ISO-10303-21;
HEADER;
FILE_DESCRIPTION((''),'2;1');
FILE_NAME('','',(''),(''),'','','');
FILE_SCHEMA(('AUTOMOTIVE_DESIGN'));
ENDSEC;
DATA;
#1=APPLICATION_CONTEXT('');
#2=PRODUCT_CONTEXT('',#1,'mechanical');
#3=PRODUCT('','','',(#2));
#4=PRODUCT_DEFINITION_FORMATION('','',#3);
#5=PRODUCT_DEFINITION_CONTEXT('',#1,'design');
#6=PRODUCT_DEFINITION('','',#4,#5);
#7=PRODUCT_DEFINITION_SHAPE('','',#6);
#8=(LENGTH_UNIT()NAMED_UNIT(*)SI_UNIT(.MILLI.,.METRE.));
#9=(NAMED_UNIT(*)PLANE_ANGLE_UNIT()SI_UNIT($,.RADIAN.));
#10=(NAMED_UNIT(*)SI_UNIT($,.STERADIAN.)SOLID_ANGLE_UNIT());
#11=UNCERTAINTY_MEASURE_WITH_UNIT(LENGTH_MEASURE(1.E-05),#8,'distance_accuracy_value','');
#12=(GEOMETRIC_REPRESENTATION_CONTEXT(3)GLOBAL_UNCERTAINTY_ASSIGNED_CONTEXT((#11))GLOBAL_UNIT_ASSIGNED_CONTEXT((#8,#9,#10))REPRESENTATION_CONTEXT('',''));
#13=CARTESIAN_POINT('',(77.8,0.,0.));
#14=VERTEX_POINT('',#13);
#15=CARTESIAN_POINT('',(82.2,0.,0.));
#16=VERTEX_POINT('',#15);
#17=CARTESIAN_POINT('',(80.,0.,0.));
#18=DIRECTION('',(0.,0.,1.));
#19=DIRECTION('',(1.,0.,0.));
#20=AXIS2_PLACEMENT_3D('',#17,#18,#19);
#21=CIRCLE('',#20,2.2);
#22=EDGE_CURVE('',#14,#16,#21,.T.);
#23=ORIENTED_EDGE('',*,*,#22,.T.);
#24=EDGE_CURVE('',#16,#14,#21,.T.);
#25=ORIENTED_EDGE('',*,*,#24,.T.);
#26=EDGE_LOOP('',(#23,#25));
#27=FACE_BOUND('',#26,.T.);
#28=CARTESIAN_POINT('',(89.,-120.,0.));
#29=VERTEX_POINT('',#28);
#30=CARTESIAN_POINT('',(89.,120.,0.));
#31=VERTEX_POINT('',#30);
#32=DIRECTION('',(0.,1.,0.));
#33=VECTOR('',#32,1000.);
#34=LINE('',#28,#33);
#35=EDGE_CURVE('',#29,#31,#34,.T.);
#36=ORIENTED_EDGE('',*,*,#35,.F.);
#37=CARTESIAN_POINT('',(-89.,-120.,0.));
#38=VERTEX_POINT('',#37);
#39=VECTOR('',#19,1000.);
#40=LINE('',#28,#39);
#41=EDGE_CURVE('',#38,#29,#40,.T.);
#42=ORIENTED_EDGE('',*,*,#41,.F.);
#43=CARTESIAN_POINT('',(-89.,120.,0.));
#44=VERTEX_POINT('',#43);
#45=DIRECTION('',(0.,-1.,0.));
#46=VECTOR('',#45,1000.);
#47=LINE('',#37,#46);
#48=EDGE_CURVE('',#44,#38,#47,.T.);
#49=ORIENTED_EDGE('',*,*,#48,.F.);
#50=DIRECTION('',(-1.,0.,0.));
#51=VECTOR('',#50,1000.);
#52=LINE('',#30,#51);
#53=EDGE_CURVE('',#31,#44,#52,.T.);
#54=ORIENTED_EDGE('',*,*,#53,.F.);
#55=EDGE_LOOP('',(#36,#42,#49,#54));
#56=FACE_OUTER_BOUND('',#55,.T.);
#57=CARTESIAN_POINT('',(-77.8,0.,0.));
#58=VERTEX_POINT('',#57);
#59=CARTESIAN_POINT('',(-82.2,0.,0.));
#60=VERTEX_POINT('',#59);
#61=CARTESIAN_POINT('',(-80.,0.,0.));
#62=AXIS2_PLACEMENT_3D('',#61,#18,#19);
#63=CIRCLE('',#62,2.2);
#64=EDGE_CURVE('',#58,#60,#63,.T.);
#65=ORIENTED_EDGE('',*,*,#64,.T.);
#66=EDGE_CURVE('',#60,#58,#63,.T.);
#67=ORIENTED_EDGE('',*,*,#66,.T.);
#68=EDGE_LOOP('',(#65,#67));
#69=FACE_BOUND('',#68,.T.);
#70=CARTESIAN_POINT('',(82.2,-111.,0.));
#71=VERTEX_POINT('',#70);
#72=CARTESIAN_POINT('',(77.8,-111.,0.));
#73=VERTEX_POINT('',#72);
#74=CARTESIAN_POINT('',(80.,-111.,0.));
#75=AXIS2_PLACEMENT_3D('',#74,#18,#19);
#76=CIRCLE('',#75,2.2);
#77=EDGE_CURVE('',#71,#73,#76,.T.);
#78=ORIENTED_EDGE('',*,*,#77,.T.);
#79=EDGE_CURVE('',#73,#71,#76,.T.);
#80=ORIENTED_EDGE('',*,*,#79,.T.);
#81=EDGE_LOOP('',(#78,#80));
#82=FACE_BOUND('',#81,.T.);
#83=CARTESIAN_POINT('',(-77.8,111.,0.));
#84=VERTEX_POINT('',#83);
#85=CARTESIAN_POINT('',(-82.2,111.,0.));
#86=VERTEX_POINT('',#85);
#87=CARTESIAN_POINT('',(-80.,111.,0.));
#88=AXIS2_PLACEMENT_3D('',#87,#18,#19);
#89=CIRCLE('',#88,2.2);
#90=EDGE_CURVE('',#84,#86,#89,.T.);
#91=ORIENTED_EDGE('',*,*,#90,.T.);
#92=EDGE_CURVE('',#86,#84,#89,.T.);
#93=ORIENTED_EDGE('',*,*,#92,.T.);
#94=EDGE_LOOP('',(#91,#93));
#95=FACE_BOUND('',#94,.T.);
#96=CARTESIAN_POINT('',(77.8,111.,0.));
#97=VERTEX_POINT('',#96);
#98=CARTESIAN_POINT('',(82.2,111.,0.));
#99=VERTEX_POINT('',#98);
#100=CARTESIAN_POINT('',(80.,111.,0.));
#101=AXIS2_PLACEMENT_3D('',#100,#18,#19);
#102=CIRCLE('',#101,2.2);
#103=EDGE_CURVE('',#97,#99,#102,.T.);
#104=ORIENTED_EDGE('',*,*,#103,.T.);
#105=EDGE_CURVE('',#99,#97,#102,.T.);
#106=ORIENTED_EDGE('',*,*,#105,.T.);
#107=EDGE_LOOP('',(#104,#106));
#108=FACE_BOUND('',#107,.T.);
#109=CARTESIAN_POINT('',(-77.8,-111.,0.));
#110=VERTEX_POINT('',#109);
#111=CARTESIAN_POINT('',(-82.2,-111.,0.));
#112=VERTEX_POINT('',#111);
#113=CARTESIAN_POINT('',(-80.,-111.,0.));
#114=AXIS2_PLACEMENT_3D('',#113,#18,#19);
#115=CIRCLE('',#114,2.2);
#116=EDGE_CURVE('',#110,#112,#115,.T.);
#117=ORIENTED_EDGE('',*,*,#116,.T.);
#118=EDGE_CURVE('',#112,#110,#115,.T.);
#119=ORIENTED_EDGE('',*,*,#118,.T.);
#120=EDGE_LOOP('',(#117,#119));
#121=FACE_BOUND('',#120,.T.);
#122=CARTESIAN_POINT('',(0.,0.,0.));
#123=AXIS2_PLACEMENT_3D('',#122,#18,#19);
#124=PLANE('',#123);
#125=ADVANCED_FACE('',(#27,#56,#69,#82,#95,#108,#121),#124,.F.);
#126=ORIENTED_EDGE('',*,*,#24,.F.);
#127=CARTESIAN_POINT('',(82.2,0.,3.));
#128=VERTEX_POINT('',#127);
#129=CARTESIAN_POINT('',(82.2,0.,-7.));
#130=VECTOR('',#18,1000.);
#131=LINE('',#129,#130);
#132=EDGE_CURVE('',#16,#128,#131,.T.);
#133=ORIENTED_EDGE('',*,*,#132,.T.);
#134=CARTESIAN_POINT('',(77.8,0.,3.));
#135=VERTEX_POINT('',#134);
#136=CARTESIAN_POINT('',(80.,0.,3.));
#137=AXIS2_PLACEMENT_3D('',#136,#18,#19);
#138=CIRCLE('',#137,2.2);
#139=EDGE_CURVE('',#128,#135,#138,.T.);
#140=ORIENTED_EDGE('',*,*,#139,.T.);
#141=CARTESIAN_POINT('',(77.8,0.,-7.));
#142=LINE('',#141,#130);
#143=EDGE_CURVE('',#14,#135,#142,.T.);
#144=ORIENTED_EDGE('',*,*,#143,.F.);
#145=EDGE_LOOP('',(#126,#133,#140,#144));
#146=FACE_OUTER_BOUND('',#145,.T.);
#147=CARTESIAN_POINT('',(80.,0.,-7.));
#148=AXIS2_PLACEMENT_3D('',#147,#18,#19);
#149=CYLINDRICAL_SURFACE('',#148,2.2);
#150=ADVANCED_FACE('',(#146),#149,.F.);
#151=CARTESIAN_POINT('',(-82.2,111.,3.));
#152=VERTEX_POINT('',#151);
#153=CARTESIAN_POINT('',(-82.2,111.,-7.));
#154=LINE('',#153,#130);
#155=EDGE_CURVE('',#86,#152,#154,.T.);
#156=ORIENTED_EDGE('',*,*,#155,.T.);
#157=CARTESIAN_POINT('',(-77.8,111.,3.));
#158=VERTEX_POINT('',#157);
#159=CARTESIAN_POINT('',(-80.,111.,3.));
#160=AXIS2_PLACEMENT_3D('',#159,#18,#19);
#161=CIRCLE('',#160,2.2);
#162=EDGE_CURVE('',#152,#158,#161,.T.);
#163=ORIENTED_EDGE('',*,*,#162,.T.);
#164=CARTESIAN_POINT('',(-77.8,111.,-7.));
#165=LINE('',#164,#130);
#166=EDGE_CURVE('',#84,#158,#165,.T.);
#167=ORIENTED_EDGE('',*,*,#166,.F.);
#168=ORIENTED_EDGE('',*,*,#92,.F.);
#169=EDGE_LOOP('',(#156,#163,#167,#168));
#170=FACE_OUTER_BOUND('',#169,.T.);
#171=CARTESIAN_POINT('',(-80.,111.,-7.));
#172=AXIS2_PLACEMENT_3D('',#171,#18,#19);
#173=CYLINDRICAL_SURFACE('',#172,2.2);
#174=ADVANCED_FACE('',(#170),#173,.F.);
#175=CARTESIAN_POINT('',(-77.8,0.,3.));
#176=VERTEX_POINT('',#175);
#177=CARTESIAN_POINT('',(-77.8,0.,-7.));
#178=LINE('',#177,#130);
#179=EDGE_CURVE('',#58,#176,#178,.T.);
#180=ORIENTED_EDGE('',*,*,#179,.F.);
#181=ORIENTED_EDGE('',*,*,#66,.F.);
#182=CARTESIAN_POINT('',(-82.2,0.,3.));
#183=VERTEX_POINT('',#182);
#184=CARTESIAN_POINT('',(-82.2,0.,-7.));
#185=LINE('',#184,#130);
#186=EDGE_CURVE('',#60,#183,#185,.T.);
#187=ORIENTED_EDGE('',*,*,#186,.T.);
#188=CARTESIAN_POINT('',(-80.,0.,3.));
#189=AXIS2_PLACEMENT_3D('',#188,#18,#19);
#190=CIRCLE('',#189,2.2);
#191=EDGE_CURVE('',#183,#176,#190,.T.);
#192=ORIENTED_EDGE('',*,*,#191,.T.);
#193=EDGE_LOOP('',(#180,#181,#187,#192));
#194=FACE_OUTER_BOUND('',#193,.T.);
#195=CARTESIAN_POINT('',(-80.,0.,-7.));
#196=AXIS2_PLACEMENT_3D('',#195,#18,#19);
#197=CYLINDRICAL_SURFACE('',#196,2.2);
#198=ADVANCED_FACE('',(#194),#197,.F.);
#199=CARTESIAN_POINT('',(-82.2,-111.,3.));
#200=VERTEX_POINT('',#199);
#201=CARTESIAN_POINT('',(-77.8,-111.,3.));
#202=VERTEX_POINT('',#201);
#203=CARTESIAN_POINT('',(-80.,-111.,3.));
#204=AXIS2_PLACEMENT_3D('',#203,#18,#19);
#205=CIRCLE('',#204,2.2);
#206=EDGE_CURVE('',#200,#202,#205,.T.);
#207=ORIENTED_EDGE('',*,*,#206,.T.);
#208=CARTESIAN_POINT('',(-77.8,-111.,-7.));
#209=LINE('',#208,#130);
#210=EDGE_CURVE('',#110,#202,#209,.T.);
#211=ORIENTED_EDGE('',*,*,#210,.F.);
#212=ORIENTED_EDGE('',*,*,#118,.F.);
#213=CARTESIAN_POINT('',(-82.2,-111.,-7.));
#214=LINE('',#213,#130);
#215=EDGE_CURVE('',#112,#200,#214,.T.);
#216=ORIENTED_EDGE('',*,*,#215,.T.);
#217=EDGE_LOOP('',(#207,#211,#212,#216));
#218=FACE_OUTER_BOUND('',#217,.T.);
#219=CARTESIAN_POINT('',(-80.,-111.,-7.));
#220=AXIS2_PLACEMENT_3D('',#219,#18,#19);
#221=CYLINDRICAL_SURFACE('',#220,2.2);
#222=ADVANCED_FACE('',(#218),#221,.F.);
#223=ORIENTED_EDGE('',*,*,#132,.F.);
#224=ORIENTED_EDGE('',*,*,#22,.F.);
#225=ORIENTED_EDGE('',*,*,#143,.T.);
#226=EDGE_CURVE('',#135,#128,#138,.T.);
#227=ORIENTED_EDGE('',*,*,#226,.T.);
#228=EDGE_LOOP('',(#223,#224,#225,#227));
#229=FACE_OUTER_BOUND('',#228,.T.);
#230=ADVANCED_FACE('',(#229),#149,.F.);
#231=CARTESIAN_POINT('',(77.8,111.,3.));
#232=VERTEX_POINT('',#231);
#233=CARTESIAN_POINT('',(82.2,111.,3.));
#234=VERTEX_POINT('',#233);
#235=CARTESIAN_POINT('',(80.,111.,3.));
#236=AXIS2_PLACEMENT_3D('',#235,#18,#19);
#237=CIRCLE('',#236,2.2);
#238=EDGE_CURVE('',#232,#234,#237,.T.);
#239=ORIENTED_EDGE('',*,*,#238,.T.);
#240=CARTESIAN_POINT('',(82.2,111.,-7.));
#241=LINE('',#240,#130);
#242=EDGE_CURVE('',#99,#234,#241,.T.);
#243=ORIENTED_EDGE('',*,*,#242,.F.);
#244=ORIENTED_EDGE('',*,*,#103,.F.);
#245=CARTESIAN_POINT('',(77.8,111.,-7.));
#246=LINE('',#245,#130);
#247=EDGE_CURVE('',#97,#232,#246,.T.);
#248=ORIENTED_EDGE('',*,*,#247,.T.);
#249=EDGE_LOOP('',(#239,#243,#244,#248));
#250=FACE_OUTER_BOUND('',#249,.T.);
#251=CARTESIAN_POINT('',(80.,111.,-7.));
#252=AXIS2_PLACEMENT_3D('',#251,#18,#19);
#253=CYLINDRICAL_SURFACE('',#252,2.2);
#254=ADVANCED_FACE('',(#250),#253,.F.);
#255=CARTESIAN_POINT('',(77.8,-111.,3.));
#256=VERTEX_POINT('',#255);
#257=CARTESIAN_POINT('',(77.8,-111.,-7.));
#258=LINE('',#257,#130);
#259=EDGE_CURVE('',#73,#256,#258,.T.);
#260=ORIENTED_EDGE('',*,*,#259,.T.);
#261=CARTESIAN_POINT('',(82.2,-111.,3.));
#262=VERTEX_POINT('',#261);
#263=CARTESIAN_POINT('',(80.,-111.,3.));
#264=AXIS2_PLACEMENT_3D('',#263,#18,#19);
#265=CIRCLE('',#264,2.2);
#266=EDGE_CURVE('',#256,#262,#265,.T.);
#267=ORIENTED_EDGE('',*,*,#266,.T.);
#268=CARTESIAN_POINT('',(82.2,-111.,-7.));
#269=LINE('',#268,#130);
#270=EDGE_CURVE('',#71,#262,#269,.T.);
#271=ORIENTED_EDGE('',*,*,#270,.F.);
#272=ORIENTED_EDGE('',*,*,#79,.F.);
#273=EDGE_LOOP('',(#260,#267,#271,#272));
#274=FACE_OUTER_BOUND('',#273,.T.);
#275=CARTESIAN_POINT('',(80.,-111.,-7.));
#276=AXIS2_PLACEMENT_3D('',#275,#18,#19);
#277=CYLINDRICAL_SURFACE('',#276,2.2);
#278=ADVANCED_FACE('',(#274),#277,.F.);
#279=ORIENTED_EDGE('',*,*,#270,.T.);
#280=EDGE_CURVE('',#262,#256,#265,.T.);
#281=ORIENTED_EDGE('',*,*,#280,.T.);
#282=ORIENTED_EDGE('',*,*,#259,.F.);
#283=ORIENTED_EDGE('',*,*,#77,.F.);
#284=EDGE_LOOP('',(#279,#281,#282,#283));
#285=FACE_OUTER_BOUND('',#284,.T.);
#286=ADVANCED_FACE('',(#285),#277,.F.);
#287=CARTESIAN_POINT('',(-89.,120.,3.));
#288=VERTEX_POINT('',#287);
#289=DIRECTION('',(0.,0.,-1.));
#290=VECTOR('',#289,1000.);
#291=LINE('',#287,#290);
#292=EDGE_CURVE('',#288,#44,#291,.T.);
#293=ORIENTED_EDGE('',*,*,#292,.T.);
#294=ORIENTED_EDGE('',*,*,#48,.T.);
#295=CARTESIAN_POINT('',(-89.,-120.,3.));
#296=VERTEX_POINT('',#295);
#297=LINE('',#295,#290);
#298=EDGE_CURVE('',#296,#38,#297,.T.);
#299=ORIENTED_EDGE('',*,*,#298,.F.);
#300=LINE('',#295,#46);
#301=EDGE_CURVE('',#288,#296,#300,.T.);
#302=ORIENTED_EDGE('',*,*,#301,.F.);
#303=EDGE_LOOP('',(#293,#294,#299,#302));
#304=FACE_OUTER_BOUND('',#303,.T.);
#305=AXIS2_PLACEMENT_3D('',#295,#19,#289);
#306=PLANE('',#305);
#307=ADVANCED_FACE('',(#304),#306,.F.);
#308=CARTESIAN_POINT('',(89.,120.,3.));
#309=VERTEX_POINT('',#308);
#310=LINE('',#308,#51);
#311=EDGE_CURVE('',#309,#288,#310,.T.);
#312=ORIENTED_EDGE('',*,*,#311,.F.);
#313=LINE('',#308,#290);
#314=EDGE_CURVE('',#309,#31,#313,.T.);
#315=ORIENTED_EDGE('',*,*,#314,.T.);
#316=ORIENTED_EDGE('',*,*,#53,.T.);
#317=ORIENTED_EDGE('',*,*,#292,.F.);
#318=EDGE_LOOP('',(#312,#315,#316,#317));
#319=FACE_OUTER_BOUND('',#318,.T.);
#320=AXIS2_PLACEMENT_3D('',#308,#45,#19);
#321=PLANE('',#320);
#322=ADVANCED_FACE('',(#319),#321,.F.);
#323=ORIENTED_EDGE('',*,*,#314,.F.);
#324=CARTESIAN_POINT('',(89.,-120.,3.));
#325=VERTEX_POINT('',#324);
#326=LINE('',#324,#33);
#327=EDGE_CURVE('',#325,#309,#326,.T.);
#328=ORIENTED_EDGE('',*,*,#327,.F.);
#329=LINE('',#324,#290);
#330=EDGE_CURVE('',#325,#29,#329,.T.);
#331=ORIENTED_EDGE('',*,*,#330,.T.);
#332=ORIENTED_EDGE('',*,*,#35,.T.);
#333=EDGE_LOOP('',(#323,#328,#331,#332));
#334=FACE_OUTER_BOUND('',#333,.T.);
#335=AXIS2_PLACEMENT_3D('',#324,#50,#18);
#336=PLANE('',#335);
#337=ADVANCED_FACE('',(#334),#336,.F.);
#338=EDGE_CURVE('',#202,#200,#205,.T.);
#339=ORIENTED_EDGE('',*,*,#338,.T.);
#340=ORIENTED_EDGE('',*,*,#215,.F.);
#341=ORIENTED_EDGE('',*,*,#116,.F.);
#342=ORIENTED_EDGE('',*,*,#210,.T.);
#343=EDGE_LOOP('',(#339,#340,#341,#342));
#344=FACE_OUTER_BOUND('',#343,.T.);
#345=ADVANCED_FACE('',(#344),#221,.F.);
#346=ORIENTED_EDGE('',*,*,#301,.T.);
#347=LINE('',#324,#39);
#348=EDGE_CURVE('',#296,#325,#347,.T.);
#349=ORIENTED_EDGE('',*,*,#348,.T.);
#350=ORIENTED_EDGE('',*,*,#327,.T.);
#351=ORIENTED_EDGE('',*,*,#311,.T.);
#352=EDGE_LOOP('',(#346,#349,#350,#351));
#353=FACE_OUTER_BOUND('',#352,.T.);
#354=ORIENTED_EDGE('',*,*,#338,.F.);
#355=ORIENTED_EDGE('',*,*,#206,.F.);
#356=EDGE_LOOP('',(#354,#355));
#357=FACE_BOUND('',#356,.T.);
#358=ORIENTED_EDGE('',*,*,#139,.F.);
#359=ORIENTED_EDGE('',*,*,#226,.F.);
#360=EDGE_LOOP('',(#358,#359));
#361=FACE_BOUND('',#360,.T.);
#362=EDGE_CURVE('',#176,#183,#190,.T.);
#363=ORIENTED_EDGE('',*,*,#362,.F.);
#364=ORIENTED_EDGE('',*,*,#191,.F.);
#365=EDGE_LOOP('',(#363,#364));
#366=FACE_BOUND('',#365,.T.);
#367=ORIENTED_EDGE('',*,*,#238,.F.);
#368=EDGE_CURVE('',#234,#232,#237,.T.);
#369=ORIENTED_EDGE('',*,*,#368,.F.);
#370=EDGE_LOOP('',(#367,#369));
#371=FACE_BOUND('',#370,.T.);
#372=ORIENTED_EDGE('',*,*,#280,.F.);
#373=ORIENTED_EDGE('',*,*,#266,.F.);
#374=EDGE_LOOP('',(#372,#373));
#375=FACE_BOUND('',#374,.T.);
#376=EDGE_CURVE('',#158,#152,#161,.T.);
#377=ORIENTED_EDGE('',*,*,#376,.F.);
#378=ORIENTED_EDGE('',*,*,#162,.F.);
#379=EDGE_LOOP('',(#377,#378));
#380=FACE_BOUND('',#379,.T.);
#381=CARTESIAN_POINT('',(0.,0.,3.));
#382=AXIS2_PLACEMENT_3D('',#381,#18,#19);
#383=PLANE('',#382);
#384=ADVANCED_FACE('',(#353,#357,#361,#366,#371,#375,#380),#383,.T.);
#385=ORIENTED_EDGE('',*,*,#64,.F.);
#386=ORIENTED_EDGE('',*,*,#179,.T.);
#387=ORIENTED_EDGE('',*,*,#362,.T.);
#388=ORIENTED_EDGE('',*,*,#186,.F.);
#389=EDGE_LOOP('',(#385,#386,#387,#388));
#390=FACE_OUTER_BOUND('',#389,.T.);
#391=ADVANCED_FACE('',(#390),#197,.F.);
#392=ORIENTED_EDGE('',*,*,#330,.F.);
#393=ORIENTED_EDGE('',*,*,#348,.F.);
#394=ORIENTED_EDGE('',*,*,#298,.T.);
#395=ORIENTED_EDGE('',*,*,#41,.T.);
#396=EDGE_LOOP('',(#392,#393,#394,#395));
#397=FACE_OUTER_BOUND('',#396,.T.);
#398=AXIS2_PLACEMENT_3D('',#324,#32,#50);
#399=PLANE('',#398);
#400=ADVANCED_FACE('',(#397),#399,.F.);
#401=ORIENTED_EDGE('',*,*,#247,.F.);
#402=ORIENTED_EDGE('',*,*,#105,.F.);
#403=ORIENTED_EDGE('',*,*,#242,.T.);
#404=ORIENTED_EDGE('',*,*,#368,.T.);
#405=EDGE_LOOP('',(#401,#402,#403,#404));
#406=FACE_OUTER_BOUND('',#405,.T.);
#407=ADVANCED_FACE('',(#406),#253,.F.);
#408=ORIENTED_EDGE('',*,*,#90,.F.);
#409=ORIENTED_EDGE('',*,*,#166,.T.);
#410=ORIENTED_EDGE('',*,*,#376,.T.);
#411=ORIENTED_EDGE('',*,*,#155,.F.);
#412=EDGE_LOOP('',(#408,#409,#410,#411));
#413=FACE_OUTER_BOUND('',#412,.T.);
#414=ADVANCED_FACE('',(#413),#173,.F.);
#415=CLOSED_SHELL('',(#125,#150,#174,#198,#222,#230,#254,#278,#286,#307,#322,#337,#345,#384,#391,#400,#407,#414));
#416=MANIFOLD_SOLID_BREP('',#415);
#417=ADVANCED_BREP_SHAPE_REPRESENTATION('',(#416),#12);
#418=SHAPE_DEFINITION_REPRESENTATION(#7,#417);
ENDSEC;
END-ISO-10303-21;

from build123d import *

# Parameters (mm, degrees)
SKETCH_1_W          = 178
SKETCH_1_H          = 240
EXTRUDE_1_DEPTH     = 3
SKETCH_2_R          = 2.2
CUT_EXTRUDE_1_DEPTH = 10


with BuildPart() as part:
    # 草图1 → 凸台-拉伸1 (new body)
    with BuildSketch(Plane.XY):
        Rectangle(SKETCH_1_W, SKETCH_1_H)
    extrude(amount=EXTRUDE_1_DEPTH)

    # 草图2 → 切除-拉伸1 (cut)
    with BuildSketch(Plane.XY.offset(3)):
        with Locations((-80, 111)):
            Circle(SKETCH_2_R)
        with Locations((80, 111)):
            Circle(SKETCH_2_R)
        with Locations((80, -111)):
            Circle(SKETCH_2_R)
        with Locations((-80, -111)):
            Circle(SKETCH_2_R)
        with Locations((-80, 0)):
            Circle(SKETCH_2_R)
        with Locations((80, 0)):
            Circle(SKETCH_2_R)
    extrude(amount=-CUT_EXTRUDE_1_DEPTH, mode=Mode.SUBTRACT)


solid = part.part
